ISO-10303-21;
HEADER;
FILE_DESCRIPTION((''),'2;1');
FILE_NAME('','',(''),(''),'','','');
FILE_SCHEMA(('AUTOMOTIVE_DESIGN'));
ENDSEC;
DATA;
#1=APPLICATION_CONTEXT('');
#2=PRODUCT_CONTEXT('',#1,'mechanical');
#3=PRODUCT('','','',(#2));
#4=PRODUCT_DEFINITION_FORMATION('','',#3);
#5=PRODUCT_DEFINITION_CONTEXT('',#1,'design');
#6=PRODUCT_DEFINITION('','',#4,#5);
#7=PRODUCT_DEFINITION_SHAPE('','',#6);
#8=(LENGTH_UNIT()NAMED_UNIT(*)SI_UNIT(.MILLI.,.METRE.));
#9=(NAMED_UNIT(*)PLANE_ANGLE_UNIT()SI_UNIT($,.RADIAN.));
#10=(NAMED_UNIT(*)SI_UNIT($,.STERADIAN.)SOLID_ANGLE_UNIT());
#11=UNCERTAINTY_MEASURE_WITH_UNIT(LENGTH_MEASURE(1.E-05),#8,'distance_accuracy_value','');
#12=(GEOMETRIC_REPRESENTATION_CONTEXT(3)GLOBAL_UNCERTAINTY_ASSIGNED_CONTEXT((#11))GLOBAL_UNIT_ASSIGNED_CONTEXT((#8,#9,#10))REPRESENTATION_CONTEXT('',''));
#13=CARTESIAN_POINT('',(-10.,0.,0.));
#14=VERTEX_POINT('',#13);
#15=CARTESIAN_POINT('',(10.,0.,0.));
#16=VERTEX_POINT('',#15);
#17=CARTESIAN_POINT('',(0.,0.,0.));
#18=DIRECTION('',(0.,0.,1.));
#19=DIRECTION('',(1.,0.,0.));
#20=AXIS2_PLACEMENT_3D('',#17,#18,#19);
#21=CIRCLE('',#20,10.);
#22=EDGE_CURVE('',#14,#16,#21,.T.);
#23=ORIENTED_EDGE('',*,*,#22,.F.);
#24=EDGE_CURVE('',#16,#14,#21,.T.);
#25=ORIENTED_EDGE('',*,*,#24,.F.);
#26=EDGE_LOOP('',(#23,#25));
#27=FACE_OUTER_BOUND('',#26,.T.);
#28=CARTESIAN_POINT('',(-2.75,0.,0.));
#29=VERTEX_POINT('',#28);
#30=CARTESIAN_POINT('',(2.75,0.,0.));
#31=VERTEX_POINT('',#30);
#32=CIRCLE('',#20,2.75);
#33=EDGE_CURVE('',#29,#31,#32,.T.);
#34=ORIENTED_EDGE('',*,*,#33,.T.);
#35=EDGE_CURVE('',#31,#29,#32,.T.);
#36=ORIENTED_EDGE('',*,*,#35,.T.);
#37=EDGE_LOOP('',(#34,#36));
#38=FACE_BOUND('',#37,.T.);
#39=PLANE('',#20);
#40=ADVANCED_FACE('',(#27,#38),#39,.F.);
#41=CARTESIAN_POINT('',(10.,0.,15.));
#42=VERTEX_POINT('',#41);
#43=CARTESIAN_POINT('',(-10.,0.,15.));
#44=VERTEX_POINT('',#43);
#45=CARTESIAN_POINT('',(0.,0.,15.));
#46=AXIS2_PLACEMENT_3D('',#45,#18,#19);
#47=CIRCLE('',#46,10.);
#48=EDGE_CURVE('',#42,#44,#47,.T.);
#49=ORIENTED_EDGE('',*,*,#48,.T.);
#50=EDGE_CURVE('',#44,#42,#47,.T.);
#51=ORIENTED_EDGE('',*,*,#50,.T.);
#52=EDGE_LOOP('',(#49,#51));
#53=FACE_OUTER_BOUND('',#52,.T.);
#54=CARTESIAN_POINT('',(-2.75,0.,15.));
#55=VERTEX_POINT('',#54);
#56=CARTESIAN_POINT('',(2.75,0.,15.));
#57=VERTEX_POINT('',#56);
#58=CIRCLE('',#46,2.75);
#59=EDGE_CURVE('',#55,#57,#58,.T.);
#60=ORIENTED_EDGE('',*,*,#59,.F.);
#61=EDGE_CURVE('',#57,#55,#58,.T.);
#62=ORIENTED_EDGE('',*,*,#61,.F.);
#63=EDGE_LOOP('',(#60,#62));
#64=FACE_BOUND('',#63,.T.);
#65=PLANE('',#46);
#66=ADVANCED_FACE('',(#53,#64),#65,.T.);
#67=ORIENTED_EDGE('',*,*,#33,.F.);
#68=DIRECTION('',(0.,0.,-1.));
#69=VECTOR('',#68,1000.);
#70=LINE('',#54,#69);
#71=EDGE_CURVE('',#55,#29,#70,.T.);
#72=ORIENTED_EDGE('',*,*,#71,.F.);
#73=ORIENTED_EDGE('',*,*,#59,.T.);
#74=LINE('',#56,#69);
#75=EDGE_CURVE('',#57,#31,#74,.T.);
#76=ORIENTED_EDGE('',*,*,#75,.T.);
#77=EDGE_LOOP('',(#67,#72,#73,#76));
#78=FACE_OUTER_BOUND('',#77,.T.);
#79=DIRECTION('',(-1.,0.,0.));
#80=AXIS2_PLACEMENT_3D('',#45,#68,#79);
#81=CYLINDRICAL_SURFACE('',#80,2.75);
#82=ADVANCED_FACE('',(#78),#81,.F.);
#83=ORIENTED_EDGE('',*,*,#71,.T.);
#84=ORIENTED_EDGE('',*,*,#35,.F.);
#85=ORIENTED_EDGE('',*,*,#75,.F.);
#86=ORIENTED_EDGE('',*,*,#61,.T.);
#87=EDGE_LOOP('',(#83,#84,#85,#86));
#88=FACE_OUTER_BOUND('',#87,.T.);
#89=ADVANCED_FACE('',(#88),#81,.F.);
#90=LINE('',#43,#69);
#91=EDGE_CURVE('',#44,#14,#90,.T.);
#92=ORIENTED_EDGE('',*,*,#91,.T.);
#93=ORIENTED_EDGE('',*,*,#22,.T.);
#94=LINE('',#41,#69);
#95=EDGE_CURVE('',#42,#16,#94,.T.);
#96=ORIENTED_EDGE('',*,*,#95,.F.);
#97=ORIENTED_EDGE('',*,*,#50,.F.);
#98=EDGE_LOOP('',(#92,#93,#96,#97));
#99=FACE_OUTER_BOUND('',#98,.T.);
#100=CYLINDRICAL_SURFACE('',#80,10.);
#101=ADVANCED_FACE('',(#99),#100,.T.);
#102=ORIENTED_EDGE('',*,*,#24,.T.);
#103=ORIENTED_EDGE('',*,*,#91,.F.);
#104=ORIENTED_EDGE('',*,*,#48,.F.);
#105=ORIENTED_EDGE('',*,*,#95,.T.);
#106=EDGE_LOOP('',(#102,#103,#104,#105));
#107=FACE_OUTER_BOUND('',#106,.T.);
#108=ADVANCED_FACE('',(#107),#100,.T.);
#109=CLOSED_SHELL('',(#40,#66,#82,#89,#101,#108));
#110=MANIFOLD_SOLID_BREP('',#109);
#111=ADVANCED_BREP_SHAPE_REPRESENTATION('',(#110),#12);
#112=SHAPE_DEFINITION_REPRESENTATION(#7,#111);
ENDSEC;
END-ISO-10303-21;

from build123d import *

# Parameters (mm, degrees)
SKETCH_1_R      = 10
SKETCH_1_R_2    = 2.75
EXTRUDE_1_DEPTH = 15


with BuildPart() as part:
    # 草图1 → 凸台-拉伸1 (new body)
    with BuildSketch(Plane.XY):
        Circle(SKETCH_1_R)
        Circle(SKETCH_1_R_2, mode=Mode.SUBTRACT)
    extrude(amount=EXTRUDE_1_DEPTH)


solid = part.part
